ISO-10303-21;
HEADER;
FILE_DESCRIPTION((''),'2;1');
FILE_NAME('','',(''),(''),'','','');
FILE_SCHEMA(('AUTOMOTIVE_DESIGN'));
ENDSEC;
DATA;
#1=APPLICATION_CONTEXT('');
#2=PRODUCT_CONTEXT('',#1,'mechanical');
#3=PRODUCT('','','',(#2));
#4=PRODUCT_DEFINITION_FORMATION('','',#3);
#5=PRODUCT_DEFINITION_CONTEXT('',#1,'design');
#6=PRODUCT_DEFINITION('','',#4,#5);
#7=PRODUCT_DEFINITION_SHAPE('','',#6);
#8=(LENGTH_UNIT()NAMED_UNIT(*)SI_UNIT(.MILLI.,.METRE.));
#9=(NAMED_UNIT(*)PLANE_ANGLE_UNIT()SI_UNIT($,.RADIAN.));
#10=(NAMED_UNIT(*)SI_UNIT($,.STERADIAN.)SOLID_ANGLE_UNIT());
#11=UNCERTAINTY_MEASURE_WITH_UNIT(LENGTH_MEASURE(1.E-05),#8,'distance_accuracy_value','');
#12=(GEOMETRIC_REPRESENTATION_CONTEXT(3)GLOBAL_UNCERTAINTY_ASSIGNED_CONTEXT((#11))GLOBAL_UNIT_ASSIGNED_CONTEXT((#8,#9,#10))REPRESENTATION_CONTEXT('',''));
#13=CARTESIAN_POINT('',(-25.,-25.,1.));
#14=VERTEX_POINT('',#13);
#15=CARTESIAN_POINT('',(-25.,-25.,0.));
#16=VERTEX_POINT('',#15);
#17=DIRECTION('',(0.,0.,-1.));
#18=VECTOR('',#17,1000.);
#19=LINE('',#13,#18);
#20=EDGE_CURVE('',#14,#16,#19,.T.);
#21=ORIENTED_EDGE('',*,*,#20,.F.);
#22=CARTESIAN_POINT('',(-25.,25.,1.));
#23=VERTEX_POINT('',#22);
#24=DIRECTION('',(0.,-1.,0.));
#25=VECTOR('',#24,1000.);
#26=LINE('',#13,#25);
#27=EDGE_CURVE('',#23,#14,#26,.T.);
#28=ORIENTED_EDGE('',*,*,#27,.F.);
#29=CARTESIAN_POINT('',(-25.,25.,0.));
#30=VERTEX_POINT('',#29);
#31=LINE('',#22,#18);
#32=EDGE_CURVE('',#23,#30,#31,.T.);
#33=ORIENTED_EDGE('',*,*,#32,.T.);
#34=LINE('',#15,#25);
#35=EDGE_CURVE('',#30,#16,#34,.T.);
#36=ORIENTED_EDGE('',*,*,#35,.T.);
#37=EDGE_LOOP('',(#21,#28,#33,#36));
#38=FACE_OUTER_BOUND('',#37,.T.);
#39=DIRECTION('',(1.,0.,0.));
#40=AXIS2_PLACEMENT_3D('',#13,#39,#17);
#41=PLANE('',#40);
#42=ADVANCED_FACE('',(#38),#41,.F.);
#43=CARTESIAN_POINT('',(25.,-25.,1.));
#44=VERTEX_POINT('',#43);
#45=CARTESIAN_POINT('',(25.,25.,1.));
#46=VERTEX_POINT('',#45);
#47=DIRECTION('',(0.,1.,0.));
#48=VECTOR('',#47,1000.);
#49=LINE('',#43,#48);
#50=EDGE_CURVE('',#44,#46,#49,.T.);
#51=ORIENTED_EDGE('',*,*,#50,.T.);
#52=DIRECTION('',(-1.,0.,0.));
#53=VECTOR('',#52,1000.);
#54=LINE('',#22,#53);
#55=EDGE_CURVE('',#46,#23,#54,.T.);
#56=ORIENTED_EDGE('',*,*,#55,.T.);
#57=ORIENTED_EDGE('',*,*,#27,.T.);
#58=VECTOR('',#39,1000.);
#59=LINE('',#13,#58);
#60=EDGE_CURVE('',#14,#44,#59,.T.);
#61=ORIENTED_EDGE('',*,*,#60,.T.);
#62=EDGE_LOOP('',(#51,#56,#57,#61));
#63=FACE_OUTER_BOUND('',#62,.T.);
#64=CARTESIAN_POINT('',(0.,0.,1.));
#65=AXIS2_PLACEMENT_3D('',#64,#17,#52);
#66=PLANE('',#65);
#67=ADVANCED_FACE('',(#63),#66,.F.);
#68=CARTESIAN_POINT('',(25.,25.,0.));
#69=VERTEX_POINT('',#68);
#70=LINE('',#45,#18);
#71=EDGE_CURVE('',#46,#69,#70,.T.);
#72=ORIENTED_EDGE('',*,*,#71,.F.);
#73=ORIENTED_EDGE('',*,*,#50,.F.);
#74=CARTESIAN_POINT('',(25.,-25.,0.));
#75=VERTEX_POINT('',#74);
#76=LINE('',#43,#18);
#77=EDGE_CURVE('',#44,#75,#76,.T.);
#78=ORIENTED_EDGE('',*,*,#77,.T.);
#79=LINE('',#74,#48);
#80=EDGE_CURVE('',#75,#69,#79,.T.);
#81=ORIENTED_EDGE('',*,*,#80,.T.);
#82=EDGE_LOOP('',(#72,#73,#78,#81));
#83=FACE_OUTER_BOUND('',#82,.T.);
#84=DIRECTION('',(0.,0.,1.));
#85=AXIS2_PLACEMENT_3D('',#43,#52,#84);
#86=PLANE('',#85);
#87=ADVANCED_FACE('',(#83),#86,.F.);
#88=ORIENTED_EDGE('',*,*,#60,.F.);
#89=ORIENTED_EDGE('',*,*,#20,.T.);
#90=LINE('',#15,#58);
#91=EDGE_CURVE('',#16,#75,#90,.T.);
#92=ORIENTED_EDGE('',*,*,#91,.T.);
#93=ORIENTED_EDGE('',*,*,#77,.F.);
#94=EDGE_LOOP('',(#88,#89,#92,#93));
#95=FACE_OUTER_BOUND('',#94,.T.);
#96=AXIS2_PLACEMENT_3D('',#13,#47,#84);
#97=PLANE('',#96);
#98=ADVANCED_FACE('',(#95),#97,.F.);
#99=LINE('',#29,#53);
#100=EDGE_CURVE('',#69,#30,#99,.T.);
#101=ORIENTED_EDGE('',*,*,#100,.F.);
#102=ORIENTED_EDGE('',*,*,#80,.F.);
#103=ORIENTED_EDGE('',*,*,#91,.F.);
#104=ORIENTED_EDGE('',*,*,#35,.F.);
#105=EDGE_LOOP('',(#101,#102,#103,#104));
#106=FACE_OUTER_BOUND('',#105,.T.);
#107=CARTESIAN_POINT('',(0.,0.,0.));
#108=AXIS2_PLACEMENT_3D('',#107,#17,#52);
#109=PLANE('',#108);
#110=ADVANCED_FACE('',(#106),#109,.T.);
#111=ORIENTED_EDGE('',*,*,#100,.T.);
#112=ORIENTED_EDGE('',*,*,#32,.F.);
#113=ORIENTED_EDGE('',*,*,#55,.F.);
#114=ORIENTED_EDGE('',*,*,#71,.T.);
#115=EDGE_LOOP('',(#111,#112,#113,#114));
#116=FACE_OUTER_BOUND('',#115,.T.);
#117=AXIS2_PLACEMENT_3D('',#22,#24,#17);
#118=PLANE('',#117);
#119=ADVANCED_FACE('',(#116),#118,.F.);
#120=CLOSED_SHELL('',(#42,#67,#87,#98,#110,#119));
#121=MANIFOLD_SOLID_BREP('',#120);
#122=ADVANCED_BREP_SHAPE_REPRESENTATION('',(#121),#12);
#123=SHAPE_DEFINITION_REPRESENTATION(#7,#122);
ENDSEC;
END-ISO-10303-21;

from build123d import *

# Parameters (mm, degrees)
SKETCH1_W           = 50
SKETCH1_H           = 50
BOSS_EXTRUDE1_DEPTH = 1


with BuildPart() as part:
    # Sketch1 → Boss-Extrude1 (new body)
    with BuildSketch(Plane.XY):
        Rectangle(SKETCH1_W, SKETCH1_H)
    extrude(amount=BOSS_EXTRUDE1_DEPTH)


solid = part.part
